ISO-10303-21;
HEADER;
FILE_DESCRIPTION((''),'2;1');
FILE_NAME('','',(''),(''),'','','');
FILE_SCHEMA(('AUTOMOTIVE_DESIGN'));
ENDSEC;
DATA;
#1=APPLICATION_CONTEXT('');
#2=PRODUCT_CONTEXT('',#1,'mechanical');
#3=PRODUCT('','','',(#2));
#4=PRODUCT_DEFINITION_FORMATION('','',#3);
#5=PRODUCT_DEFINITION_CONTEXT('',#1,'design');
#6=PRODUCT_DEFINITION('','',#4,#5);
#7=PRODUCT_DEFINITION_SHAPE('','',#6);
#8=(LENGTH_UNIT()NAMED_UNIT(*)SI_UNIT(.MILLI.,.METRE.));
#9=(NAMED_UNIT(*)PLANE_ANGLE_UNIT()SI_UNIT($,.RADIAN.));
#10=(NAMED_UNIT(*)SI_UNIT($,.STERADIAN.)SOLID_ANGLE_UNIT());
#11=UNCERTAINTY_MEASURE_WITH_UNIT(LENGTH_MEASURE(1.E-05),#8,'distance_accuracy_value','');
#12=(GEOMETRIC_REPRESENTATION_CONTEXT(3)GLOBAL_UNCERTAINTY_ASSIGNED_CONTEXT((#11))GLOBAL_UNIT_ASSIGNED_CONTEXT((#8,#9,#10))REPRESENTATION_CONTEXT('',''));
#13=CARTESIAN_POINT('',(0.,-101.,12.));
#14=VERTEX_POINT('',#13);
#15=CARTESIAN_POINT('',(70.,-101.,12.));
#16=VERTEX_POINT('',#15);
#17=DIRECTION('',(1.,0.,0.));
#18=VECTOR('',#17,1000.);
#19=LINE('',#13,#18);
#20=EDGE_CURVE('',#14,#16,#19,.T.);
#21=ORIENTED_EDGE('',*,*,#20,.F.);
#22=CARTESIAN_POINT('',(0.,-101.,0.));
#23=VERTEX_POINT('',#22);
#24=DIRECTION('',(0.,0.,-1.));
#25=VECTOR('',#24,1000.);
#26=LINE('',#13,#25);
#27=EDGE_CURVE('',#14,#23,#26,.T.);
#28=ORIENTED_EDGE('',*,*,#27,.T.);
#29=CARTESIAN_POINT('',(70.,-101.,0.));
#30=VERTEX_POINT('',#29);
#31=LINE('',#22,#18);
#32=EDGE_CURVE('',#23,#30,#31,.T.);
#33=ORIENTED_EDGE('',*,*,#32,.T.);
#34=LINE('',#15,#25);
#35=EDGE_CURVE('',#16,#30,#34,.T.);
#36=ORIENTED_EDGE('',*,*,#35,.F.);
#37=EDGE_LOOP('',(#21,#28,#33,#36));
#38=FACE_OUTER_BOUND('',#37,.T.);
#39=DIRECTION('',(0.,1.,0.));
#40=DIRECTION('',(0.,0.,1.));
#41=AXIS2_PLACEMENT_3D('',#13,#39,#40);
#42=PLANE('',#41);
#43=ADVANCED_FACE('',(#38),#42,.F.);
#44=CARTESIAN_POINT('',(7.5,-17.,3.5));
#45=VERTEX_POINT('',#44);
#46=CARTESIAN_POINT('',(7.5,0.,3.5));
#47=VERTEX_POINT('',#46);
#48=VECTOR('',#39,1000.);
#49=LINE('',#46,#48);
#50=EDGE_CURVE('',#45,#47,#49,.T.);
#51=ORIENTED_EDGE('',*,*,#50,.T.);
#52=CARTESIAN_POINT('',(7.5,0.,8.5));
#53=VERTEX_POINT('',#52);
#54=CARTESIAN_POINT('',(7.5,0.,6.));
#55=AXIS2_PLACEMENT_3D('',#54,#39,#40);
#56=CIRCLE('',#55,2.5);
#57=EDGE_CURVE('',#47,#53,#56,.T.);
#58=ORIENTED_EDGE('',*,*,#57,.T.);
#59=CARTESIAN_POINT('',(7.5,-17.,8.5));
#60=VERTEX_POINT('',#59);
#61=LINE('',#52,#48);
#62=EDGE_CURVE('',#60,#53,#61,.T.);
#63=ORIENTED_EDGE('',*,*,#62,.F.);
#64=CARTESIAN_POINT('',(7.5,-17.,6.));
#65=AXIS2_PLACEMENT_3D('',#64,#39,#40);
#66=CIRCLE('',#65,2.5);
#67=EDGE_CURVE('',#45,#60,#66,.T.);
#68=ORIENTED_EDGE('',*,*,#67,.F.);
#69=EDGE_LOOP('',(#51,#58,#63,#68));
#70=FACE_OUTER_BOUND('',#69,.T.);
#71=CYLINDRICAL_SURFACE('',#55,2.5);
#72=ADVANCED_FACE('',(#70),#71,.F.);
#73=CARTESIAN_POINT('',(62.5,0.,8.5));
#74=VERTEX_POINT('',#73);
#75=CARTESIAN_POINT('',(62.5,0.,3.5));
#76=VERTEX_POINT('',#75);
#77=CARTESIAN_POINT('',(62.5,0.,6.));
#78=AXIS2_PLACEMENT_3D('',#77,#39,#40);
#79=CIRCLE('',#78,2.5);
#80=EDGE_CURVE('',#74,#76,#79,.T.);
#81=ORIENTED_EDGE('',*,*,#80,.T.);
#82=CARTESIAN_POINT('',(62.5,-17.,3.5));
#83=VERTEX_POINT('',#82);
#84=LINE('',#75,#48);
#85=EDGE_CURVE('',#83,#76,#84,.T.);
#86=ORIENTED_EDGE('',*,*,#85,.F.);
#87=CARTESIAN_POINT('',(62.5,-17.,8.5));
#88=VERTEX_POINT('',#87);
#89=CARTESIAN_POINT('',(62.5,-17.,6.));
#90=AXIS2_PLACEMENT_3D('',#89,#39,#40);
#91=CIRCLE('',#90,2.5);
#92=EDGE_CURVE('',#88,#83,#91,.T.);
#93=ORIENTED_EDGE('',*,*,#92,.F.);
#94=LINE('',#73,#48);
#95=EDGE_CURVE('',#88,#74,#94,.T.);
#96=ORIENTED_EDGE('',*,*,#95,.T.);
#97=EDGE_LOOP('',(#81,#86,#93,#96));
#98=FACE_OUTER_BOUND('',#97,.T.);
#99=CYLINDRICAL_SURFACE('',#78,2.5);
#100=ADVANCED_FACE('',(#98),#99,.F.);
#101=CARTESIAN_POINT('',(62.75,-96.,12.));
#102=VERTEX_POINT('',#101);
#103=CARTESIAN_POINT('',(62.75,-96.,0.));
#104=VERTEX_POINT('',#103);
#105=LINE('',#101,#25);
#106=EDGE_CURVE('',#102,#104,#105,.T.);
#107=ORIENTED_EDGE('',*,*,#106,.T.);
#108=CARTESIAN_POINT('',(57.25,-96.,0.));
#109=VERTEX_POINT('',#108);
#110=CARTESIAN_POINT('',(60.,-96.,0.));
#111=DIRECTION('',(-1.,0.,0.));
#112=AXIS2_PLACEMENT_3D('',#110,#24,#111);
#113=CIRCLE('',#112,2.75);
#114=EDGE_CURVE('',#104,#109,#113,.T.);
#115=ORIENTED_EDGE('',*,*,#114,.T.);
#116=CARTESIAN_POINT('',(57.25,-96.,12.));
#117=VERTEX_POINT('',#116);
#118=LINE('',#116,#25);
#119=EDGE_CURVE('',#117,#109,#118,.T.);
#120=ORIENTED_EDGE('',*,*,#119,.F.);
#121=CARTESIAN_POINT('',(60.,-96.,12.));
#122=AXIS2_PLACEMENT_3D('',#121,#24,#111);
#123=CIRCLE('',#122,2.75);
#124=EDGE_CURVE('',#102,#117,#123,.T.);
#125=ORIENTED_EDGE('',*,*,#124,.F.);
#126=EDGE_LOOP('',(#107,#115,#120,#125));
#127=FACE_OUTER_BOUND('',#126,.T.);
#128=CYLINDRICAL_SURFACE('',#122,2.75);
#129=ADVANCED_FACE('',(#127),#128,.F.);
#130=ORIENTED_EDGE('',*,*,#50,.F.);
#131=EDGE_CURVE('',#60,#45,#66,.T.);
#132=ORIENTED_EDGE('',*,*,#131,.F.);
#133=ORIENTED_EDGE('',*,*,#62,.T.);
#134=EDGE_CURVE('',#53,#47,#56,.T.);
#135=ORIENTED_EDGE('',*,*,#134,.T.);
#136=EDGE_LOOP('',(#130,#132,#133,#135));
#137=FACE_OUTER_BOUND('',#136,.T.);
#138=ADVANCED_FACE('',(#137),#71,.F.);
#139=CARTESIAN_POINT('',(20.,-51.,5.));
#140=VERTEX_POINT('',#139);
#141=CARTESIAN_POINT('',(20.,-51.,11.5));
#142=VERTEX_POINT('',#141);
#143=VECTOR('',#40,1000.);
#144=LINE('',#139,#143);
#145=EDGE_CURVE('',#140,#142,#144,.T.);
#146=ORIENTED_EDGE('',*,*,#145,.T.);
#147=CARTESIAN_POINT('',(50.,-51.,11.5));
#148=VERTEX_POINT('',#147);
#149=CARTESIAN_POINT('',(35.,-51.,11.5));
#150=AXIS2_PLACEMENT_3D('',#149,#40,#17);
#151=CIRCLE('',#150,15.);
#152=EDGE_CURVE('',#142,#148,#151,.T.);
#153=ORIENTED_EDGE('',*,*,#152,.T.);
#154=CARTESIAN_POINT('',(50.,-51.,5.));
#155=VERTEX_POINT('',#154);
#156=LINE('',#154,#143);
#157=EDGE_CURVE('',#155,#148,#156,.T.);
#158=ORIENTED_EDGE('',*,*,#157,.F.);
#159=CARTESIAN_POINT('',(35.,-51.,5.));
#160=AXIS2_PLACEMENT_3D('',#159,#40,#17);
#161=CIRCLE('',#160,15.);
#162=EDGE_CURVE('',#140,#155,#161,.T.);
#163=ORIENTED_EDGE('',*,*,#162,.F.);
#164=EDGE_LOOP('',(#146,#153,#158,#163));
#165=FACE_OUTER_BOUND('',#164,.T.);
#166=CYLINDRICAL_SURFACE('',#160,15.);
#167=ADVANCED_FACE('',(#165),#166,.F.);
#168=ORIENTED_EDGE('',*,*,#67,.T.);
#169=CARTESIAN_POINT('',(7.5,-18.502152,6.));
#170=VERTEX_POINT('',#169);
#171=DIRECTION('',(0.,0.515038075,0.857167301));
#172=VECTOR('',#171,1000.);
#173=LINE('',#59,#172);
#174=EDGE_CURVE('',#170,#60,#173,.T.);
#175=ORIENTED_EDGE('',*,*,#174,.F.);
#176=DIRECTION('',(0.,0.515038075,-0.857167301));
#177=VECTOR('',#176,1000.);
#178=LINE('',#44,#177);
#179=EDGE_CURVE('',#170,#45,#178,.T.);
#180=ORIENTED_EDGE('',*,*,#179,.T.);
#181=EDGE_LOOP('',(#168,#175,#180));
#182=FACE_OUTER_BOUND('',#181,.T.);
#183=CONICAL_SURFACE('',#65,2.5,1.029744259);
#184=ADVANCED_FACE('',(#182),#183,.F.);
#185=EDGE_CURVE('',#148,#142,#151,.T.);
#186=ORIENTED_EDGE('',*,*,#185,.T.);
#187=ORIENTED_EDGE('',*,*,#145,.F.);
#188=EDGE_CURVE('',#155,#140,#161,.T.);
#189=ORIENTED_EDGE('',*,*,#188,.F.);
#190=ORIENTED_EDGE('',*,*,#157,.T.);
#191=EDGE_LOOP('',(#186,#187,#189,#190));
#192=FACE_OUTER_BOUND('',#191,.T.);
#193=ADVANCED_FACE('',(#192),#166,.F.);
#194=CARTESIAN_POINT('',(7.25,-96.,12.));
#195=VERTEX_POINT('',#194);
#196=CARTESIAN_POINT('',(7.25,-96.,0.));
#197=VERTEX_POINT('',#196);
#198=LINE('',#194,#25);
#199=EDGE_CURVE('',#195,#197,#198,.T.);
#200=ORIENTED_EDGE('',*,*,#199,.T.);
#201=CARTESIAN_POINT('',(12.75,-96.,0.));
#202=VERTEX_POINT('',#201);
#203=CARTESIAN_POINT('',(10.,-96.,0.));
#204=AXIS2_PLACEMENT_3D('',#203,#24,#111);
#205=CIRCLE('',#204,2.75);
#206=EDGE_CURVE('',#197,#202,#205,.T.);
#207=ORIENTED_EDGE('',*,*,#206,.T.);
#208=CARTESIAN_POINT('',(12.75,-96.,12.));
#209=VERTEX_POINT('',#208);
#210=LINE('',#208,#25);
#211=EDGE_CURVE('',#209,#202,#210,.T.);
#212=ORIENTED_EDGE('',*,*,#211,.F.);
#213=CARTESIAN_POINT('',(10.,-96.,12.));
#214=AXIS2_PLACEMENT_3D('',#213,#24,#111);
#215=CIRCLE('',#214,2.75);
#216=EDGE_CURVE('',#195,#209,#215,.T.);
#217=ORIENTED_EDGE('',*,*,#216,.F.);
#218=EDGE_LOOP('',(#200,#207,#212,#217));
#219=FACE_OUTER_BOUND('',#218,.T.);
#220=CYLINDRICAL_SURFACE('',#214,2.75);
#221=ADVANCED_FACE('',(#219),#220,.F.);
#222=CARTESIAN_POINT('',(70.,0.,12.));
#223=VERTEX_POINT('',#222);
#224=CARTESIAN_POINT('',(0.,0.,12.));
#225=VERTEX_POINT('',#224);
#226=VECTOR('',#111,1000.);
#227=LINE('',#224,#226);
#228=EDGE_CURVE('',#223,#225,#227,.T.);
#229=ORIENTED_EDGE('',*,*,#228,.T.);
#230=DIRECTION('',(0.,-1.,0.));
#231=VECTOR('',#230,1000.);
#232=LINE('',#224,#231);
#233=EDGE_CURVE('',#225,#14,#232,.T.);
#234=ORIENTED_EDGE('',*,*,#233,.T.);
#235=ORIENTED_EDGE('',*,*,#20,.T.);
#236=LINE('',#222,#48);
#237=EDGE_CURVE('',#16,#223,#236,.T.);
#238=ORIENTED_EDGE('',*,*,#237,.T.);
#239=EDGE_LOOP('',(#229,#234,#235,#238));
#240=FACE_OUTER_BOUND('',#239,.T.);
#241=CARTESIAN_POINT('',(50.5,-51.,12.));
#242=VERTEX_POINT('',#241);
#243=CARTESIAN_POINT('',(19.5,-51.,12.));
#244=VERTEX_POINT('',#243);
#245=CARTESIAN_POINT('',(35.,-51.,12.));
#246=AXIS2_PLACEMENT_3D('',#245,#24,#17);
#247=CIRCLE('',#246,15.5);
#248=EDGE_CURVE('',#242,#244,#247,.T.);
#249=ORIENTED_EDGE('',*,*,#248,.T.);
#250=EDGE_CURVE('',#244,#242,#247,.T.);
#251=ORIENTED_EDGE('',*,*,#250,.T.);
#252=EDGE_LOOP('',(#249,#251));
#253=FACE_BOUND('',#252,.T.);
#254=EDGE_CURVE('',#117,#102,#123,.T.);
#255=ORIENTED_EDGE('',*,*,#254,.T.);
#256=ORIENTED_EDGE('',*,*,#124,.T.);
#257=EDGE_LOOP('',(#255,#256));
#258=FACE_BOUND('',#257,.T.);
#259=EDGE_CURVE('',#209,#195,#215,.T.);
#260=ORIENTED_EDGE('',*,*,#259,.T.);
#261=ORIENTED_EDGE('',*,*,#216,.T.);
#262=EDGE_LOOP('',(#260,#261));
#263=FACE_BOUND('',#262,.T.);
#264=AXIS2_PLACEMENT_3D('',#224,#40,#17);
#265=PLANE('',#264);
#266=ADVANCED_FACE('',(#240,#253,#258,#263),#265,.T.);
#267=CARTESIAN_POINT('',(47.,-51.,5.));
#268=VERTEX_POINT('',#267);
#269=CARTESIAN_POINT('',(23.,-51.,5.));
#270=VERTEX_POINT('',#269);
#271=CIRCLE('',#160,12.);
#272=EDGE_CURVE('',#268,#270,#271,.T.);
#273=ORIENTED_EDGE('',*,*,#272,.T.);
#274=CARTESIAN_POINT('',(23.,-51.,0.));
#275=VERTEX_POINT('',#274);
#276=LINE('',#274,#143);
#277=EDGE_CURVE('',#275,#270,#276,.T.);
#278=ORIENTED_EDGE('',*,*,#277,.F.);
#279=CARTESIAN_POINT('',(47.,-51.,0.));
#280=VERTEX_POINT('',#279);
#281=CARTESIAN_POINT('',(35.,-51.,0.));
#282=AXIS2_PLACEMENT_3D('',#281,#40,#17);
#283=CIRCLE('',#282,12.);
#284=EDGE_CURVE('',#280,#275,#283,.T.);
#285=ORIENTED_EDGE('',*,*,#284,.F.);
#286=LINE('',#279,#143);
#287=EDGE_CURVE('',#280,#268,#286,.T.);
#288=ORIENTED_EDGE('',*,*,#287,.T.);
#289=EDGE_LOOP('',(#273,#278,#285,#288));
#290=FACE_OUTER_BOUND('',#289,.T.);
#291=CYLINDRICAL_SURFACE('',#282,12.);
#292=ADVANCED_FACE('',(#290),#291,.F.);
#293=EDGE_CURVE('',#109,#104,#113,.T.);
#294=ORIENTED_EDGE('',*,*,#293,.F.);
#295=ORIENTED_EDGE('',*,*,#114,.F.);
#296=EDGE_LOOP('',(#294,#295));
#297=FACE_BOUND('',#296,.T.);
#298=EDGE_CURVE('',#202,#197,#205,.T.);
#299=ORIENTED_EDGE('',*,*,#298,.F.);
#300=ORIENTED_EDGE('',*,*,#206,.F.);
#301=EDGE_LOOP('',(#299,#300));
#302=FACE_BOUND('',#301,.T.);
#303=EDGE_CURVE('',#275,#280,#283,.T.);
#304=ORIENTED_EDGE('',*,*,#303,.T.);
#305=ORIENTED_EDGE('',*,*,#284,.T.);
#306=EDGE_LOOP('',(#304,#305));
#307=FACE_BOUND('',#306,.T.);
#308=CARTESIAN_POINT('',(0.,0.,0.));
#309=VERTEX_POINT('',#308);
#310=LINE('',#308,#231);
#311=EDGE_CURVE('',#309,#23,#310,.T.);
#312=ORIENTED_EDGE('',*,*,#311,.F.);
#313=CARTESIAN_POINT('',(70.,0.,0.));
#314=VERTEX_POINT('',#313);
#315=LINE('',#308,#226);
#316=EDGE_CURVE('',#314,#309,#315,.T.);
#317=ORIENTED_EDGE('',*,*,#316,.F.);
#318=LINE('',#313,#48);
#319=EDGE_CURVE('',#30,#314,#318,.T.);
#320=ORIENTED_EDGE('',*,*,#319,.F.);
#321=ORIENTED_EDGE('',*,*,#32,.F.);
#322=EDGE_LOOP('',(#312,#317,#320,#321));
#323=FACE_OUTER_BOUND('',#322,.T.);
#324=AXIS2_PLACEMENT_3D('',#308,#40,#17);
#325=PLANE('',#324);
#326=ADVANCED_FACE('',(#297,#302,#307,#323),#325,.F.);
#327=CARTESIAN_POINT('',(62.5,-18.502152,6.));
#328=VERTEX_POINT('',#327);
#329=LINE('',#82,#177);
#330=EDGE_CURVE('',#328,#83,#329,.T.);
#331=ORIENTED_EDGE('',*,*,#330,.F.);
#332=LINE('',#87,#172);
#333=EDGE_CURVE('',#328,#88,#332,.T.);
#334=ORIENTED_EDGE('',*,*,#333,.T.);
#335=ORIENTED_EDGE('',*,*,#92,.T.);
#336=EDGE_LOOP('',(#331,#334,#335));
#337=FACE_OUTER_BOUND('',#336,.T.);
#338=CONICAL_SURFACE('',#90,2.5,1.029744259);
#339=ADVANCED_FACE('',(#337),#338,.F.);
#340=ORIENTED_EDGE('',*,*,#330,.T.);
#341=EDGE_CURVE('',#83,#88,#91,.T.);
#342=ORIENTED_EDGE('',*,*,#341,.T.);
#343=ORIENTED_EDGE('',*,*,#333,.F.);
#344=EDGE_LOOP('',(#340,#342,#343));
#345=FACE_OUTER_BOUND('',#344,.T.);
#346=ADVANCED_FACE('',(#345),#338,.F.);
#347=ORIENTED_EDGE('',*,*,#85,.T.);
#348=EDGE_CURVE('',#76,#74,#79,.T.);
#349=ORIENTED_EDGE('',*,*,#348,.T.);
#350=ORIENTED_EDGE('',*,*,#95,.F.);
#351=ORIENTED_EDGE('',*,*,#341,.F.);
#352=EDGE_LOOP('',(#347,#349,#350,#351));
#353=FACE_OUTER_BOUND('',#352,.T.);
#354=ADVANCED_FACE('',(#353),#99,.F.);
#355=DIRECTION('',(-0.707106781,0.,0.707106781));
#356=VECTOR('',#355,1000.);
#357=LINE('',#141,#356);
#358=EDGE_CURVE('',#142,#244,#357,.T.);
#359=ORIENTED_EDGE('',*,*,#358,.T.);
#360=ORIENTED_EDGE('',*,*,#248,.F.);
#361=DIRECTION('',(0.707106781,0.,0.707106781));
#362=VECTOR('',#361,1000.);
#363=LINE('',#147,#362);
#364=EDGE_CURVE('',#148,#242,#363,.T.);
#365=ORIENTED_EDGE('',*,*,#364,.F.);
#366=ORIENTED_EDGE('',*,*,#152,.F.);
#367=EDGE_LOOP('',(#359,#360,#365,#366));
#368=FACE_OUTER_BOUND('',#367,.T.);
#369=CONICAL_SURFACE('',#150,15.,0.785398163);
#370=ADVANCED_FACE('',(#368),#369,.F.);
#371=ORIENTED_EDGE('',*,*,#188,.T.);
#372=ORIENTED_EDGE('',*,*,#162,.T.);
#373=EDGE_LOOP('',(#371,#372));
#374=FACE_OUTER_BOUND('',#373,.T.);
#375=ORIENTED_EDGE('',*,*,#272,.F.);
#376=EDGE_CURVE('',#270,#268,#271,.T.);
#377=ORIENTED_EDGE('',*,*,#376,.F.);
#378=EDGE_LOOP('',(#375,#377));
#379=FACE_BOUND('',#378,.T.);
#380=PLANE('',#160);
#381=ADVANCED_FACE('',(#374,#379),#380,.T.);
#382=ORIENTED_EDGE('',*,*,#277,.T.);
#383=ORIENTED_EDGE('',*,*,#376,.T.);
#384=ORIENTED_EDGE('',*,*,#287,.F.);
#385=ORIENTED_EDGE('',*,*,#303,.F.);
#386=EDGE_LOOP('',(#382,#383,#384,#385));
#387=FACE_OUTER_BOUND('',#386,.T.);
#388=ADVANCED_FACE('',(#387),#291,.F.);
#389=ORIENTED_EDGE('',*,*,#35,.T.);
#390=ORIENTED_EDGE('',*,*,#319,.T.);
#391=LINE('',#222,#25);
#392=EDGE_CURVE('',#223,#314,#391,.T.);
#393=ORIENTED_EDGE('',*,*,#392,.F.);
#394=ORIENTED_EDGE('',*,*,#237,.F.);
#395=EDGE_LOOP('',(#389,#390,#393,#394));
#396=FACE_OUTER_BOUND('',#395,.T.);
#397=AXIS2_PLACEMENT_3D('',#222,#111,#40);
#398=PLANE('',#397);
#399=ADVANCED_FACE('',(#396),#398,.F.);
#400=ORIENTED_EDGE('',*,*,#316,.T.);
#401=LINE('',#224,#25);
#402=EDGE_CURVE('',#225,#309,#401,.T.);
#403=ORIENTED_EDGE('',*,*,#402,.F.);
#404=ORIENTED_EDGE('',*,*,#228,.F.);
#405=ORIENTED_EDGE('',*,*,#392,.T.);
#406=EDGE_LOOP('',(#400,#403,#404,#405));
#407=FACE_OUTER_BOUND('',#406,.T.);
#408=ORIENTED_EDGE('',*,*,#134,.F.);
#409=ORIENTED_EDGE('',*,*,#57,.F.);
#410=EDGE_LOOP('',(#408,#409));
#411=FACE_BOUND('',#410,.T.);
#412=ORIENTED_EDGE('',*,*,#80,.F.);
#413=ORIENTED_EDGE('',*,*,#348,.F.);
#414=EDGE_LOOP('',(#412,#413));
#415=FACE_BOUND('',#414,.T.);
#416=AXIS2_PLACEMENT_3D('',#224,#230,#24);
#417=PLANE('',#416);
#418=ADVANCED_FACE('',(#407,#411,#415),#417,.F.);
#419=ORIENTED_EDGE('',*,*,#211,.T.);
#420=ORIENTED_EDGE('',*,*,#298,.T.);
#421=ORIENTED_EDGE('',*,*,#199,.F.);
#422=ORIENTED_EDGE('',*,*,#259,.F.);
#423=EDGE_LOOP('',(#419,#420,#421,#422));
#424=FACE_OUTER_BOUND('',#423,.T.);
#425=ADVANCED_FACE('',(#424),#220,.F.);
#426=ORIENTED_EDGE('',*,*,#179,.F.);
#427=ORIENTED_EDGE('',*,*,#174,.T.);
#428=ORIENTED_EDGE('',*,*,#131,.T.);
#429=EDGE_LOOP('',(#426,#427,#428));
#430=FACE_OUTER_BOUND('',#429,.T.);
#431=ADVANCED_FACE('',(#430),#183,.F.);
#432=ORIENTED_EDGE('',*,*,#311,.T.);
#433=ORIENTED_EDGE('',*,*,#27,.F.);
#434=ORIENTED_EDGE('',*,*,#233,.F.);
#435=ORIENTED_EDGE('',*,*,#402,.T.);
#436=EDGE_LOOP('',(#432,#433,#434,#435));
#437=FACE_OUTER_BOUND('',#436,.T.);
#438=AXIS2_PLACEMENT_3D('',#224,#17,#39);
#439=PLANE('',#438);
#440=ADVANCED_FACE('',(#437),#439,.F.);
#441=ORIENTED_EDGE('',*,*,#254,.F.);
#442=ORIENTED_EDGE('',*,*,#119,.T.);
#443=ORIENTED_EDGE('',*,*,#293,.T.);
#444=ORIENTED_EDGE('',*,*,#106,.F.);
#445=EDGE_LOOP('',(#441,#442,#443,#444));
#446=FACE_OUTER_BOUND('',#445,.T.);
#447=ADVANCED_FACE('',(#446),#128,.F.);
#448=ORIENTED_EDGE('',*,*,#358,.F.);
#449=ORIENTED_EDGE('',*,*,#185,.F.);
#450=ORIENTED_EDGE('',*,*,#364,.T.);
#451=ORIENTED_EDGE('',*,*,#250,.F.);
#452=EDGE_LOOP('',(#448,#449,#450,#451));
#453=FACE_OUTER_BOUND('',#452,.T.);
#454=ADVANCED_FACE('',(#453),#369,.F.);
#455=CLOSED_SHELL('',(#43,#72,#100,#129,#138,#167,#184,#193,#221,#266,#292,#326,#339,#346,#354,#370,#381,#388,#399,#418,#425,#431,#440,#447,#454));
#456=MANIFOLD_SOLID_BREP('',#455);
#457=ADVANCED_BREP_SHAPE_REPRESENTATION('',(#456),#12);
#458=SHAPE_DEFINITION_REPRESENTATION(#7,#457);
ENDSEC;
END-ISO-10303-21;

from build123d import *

# Parameters (mm, degrees)
SKETCH_1_W             = 70
SKETCH_1_H             = 101
EXTRUDE_1_DEPTH        = 12
SKETCH_2_R             = 15
CUT_EXTRUDE_1_DEPTH    = 7
SKETCH_3_R             = 12
CUT_EXTRUDE_2_DEPTH    = 124.085336251
CHAMFER_2_SIZE         = 0.5
HOLE_WIZARD_M6_1_D     = 5
HOLE_WIZARD_M6_1_DEPTH = 17
HOLE_WIZARD_M6_1_TIP   = 1.502151548
SKETCH_10_R            = 2.75
CUT_EXTRUDE_3_DEPTH    = 124.470644284


with BuildPart() as part:
    # 草图1 → 凸台-拉伸1 (new body)
    with BuildSketch(Plane.XY):
        with Locations((35, -50.5)):
            Rectangle(SKETCH_1_W, SKETCH_1_H)
    extrude(amount=EXTRUDE_1_DEPTH)

    # 草图2 → 切除-拉伸1 (cut)
    with BuildSketch(Plane.XY.offset(12)):
        with Locations((35, -51)):
            Circle(SKETCH_2_R)
    extrude(amount=-CUT_EXTRUDE_1_DEPTH, mode=Mode.SUBTRACT)

    # 草图3 → 切除-拉伸2 (cut, through all)
    with BuildSketch(Plane.XY.offset(5)):
        with Locations((35, -51)):
            Circle(SKETCH_3_R)
    extrude(amount=-CUT_EXTRUDE_2_DEPTH, mode=Mode.SUBTRACT)

    # 倒角2
    chamfer_2_edges = [part.edges().sort_by_distance(p)[0] for p in [
        (20, -51, 12),
    ]]
    chamfer(chamfer_2_edges, length=CHAMFER_2_SIZE)

    # M6 螺纹孔1
    with Locations(Plane(origin=(0, 0, 0), x_dir=(1, 0, 0), z_dir=(0, 1, 0))):
        with Locations((62.5, -6), (7.5, -6)):
            Hole(HOLE_WIZARD_M6_1_D / 2, depth=HOLE_WIZARD_M6_1_DEPTH)
            with Locations((0, 0, -(HOLE_WIZARD_M6_1_DEPTH + HOLE_WIZARD_M6_1_TIP / 2))):  # 118° drill point
                Cone(0, HOLE_WIZARD_M6_1_D / 2, HOLE_WIZARD_M6_1_TIP, mode=Mode.SUBTRACT)

    # 草图10 → 切除-拉伸3 (cut, through all)
    with BuildSketch(Plane(origin=(0, 0, 0), x_dir=(-1, 0, 0), z_dir=(0, 0, -1))):
        with Locations((-60, -96)):
            Circle(SKETCH_10_R)
        with Locations((-10, -96)):
            Circle(SKETCH_10_R)
    extrude(amount=-CUT_EXTRUDE_3_DEPTH, mode=Mode.SUBTRACT)


solid = part.part
